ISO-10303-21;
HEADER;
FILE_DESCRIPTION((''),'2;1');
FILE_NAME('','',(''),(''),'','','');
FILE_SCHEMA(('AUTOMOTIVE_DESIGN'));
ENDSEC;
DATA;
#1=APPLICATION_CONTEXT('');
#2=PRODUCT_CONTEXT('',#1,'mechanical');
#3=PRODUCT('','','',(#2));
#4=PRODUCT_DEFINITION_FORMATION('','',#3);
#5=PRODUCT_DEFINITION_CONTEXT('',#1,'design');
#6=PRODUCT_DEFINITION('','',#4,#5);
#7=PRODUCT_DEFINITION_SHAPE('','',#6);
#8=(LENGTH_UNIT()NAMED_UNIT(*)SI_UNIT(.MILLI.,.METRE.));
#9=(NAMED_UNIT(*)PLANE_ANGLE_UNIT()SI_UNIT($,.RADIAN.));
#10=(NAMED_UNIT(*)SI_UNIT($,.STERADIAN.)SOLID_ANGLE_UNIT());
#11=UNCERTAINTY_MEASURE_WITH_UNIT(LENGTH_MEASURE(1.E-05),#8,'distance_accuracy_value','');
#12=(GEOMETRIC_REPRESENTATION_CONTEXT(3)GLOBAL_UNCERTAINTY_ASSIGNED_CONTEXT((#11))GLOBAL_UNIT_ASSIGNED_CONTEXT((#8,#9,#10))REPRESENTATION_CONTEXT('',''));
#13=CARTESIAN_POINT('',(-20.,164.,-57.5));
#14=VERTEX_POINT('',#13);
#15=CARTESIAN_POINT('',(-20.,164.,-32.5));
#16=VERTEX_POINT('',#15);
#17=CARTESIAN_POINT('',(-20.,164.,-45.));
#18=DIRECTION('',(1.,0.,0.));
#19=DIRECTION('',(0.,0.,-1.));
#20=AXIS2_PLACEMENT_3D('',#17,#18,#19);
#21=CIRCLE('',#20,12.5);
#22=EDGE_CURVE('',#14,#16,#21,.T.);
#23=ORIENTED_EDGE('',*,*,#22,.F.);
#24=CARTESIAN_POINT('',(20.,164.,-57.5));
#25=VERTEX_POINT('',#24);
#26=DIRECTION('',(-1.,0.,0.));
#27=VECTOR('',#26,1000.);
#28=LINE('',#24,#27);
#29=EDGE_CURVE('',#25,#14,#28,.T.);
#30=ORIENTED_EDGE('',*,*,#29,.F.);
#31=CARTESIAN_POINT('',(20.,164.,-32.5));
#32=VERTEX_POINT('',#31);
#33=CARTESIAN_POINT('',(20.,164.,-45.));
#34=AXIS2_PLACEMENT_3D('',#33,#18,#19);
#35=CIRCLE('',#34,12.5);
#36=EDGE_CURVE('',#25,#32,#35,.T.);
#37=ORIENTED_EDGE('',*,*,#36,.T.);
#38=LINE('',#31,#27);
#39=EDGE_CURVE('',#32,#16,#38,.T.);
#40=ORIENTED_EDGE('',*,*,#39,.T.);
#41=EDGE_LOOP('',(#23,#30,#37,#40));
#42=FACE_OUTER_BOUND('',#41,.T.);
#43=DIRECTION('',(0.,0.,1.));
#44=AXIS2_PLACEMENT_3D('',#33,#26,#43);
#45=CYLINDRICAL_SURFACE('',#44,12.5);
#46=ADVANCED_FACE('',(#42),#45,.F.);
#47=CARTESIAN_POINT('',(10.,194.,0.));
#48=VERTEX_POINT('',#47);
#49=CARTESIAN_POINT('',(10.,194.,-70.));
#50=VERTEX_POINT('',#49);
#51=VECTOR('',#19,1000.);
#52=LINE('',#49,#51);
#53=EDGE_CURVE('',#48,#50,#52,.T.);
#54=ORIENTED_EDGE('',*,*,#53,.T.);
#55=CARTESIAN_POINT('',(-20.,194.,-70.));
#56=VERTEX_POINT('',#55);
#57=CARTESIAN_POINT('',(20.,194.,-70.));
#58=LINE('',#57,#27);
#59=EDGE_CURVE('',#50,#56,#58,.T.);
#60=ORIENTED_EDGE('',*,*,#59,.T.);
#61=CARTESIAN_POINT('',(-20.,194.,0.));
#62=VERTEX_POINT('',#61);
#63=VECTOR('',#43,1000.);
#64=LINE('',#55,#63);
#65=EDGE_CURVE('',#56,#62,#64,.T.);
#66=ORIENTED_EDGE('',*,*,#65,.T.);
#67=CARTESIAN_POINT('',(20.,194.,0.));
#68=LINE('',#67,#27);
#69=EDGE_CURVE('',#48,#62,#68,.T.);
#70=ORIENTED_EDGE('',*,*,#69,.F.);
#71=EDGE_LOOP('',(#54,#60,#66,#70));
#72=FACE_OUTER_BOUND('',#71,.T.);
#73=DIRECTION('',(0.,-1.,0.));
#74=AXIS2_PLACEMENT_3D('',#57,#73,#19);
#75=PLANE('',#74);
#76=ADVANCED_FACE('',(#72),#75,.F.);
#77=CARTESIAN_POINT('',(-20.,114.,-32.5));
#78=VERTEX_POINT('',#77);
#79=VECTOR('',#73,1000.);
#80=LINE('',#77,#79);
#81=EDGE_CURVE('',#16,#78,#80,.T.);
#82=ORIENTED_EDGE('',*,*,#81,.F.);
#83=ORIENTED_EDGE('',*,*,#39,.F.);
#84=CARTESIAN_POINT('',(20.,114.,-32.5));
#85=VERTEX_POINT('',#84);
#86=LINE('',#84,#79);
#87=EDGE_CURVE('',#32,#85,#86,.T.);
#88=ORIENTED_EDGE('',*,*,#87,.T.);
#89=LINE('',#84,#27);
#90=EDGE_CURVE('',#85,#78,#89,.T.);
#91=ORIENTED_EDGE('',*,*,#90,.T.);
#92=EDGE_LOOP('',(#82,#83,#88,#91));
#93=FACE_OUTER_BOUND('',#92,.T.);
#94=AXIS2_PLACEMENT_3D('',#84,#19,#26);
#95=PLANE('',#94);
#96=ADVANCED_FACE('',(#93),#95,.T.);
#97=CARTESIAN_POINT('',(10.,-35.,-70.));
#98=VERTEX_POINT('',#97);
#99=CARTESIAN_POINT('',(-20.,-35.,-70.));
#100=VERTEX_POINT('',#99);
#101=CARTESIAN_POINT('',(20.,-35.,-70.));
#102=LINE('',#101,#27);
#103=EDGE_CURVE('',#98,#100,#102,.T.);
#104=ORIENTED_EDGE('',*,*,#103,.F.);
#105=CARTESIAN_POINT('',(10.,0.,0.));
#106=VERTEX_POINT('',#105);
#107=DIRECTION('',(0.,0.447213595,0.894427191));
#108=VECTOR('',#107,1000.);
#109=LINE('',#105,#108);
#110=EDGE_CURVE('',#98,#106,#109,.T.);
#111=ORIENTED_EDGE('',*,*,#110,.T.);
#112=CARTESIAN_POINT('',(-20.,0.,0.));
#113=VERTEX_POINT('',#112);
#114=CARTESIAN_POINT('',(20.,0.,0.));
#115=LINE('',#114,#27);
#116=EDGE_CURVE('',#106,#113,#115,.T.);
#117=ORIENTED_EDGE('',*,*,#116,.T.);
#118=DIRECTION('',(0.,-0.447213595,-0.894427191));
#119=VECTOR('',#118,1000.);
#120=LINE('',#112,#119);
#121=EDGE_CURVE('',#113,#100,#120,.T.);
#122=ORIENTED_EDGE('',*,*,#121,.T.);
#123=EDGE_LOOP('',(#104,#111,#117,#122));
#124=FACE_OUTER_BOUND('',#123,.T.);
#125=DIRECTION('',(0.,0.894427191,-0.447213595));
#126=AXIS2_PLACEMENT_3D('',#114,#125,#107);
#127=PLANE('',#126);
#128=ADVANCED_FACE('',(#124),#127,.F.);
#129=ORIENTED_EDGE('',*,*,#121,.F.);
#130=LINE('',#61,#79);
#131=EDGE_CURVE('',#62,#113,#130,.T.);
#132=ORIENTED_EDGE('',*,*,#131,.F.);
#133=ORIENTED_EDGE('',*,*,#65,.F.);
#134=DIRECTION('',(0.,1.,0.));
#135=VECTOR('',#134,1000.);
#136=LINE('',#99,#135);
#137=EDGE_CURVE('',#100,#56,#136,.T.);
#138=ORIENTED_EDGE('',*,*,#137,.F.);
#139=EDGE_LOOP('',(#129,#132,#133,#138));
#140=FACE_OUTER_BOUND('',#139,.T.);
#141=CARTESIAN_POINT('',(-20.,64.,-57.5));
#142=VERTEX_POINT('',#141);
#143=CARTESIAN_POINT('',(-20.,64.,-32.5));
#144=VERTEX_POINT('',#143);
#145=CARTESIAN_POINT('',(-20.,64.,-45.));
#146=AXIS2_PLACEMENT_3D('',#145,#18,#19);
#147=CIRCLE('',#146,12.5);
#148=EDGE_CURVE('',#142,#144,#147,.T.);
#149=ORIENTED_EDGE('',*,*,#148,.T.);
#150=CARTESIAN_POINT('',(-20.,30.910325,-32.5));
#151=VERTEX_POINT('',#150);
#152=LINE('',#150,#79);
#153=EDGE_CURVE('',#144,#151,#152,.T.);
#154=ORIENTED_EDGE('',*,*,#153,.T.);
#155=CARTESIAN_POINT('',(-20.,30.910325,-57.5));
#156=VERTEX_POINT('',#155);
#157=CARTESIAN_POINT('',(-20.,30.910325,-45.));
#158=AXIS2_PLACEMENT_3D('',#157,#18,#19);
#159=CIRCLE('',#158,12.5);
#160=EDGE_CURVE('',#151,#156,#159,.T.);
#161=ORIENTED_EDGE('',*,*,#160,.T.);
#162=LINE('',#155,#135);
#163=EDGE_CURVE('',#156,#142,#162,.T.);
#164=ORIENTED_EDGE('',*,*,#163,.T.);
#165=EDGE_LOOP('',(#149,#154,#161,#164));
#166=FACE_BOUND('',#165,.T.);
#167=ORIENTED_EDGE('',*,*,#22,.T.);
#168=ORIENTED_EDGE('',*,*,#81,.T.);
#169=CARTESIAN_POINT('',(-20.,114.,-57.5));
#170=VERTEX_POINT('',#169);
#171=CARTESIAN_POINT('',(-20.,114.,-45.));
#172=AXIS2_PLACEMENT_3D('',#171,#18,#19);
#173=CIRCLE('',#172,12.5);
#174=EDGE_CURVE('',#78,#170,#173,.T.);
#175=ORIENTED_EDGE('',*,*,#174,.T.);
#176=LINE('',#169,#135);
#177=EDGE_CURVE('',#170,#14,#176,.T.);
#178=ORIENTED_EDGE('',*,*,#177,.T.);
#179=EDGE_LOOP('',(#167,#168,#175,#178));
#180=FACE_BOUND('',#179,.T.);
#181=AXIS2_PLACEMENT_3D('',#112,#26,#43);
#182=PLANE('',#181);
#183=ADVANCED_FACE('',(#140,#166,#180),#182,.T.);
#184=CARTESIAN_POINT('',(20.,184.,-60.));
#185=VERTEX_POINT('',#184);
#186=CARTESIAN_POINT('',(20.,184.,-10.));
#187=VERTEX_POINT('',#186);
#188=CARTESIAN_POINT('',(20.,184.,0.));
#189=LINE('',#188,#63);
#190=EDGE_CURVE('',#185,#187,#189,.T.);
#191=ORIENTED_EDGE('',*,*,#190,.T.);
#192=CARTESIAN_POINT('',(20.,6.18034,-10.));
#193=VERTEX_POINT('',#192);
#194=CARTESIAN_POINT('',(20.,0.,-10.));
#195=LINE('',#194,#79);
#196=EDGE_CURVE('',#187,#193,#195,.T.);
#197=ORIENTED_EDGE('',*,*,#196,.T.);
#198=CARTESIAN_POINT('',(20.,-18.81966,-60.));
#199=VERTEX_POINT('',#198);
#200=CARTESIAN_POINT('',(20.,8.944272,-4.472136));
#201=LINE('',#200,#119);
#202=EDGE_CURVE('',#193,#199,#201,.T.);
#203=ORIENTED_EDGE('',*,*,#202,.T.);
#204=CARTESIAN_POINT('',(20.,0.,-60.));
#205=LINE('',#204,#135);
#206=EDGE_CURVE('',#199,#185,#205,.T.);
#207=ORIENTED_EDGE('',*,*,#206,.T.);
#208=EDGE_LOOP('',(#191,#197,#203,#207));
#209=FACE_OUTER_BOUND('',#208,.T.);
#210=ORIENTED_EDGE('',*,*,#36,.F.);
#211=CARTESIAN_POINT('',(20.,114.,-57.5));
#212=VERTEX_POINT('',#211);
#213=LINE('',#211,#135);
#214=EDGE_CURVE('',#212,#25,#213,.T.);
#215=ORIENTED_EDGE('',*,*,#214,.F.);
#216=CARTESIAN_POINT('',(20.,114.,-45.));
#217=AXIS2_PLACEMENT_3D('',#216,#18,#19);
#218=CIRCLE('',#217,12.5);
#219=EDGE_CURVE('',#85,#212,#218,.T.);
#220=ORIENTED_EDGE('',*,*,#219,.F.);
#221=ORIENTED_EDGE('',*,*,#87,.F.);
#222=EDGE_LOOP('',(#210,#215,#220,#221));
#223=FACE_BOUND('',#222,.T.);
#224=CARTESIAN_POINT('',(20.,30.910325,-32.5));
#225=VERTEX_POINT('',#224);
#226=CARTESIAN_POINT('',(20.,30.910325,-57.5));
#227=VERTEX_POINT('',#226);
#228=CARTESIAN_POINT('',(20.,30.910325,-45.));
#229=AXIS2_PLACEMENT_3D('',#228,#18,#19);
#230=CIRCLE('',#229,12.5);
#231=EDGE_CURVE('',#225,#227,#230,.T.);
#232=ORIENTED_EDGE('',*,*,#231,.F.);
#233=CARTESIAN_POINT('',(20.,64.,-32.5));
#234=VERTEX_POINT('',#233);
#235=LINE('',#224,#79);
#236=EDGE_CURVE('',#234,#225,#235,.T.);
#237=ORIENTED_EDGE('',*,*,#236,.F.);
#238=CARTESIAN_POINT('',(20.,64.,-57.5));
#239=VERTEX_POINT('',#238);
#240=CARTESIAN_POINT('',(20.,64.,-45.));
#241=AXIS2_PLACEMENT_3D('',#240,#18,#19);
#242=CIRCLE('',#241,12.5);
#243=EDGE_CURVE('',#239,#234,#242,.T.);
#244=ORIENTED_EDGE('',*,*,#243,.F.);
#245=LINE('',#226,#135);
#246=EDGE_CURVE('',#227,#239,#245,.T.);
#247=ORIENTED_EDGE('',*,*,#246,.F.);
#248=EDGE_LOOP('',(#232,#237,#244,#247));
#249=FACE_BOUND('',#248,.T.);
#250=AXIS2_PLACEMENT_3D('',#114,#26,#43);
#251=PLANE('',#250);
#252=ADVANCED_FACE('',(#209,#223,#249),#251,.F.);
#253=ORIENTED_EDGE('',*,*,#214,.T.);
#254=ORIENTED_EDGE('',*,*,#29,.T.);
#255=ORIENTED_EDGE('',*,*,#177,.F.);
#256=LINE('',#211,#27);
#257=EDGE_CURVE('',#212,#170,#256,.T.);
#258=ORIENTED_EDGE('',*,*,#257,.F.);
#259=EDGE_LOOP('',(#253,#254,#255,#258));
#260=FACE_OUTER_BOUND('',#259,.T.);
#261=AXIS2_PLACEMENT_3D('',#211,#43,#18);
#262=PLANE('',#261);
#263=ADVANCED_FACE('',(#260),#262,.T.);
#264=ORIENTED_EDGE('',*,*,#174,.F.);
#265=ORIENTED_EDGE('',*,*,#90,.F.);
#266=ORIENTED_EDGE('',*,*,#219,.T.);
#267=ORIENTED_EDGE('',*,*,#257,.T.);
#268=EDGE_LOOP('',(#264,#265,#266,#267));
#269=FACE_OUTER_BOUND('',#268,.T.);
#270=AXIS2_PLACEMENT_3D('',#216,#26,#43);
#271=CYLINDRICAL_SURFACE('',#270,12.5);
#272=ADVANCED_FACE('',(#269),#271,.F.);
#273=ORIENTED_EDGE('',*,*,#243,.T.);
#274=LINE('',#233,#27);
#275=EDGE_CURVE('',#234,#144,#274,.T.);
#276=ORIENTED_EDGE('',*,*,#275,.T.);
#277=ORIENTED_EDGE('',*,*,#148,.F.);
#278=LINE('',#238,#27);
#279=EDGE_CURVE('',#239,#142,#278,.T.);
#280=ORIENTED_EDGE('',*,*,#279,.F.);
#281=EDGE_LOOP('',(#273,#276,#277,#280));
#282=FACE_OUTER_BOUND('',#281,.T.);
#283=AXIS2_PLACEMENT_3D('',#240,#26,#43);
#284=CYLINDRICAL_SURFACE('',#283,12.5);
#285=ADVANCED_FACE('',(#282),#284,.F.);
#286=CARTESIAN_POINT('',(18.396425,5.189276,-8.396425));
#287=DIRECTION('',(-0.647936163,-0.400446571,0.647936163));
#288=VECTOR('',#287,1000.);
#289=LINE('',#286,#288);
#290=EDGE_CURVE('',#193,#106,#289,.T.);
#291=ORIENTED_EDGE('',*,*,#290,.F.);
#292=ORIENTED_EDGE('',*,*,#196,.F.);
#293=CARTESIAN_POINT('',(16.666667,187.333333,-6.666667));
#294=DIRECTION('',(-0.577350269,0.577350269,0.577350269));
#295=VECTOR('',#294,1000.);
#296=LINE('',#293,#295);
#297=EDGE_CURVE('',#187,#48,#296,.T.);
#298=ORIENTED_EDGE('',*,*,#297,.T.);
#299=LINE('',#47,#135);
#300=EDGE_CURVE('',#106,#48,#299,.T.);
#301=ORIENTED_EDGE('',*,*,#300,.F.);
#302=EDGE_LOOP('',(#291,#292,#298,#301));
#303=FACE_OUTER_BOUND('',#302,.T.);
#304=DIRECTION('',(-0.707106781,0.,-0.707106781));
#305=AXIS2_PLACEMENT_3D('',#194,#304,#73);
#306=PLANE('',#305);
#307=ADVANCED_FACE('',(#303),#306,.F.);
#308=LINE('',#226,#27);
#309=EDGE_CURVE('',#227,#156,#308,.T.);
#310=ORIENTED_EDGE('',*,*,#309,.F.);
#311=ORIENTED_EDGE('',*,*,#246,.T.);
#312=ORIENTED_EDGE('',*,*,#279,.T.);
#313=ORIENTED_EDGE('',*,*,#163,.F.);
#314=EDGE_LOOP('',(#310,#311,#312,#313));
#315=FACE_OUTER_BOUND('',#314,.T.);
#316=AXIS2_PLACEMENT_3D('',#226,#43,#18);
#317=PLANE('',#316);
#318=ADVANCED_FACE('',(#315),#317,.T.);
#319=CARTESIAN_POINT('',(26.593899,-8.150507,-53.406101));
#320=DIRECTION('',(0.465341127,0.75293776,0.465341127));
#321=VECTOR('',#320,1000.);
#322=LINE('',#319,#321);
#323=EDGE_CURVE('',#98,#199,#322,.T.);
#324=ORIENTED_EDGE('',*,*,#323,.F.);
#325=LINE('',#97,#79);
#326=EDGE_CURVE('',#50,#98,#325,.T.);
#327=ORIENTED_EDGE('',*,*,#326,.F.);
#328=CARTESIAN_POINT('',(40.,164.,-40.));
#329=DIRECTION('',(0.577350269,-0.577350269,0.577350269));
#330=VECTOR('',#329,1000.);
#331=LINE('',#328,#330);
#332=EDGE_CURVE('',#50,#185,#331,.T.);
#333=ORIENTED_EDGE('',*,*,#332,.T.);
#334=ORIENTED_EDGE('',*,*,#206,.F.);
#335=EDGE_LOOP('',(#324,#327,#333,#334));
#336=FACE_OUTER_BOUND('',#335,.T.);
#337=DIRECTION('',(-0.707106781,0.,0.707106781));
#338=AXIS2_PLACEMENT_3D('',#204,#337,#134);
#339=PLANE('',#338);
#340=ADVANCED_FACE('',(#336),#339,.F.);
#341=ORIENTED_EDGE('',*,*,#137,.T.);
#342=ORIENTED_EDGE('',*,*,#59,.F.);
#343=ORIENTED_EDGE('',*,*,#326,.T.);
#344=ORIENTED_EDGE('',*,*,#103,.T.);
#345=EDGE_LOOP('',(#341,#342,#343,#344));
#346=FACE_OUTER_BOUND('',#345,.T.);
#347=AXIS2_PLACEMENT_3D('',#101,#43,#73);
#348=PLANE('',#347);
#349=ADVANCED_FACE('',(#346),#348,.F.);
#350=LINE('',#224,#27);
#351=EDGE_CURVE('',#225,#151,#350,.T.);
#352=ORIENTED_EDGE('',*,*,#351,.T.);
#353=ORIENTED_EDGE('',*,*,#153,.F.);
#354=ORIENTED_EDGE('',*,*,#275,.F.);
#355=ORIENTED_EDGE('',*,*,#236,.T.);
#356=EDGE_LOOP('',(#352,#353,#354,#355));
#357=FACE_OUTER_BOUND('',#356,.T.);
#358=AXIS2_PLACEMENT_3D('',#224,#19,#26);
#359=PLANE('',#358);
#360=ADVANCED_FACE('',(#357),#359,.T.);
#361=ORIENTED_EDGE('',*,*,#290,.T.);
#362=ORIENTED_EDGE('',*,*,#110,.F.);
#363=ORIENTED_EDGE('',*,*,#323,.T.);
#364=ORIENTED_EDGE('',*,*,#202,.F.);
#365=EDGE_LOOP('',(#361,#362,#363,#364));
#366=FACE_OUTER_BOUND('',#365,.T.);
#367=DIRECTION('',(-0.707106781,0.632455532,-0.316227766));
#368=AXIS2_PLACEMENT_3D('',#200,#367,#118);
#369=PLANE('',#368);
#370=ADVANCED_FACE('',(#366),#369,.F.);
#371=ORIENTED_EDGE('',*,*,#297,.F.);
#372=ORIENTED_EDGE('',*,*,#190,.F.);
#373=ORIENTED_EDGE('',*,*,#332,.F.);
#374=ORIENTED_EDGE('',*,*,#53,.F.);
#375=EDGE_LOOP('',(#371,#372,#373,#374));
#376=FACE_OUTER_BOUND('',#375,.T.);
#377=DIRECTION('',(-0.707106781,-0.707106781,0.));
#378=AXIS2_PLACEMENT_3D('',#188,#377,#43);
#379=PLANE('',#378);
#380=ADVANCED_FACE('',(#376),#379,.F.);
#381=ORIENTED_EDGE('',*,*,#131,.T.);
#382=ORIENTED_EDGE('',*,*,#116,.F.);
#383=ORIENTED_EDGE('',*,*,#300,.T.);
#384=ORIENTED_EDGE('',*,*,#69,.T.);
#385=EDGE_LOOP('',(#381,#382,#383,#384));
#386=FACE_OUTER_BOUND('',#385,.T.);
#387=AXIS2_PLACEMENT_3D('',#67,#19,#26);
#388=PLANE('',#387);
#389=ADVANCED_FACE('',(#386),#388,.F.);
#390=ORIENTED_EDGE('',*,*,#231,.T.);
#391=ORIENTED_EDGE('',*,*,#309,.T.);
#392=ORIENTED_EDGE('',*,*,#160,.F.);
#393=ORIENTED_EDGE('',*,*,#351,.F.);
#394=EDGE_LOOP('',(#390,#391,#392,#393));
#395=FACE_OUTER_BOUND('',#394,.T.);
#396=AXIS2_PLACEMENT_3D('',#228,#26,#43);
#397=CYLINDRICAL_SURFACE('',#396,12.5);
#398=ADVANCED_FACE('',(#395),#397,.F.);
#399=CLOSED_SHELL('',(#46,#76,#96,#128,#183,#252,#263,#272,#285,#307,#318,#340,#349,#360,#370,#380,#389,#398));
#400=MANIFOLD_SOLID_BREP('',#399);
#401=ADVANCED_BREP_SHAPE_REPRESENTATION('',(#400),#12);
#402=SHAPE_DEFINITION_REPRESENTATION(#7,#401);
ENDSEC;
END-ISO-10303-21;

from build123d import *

# Parameters (mm, degrees)
BOSS_EXTRUDE1_DEPTH = 20
CHAMFER1_SIZE       = 10


with BuildPart() as part:
    # Sketch1 → Boss-Extrude1 (new, symmetric)
    with BuildSketch(Plane(origin=(0, 0, 0), x_dir=(0, 0, -1), z_dir=(1, 0, 0))):
        Polygon((0, 0), (70, -35), (70, 194), (0, 194), align=None)
        with BuildLine():
            Line((32.5, 114), (32.5, 164))
            ThreePointArc((32.5, 164), (45, 176.5), (57.5, 164))
            Line((57.5, 164), (57.5, 114))
            ThreePointArc((57.5, 114), (45, 101.5), (32.5, 114))
        make_face(mode=Mode.SUBTRACT)
        with BuildLine():
            Line((32.5, 30.910324642), (32.5, 64))
            ThreePointArc((32.5, 64), (45, 76.5), (57.5, 64))
            Line((57.5, 64), (57.5, 30.910324642))
            ThreePointArc((57.5, 30.910324642), (45, 18.410324642), (32.5, 30.910324642))
        make_face(mode=Mode.SUBTRACT)
    extrude(amount=BOSS_EXTRUDE1_DEPTH, both=True)

    # Chamfer1
    chamfer1_edges = [part.edges().sort_by_distance(p)[0] for p in [
        (20, 79.5, -70),
        (20, 194, -35),
        (20, 97, 0),
        (20, -17.5, -35),
    ]]
    chamfer(chamfer1_edges, length=CHAMFER1_SIZE)


solid = part.part
